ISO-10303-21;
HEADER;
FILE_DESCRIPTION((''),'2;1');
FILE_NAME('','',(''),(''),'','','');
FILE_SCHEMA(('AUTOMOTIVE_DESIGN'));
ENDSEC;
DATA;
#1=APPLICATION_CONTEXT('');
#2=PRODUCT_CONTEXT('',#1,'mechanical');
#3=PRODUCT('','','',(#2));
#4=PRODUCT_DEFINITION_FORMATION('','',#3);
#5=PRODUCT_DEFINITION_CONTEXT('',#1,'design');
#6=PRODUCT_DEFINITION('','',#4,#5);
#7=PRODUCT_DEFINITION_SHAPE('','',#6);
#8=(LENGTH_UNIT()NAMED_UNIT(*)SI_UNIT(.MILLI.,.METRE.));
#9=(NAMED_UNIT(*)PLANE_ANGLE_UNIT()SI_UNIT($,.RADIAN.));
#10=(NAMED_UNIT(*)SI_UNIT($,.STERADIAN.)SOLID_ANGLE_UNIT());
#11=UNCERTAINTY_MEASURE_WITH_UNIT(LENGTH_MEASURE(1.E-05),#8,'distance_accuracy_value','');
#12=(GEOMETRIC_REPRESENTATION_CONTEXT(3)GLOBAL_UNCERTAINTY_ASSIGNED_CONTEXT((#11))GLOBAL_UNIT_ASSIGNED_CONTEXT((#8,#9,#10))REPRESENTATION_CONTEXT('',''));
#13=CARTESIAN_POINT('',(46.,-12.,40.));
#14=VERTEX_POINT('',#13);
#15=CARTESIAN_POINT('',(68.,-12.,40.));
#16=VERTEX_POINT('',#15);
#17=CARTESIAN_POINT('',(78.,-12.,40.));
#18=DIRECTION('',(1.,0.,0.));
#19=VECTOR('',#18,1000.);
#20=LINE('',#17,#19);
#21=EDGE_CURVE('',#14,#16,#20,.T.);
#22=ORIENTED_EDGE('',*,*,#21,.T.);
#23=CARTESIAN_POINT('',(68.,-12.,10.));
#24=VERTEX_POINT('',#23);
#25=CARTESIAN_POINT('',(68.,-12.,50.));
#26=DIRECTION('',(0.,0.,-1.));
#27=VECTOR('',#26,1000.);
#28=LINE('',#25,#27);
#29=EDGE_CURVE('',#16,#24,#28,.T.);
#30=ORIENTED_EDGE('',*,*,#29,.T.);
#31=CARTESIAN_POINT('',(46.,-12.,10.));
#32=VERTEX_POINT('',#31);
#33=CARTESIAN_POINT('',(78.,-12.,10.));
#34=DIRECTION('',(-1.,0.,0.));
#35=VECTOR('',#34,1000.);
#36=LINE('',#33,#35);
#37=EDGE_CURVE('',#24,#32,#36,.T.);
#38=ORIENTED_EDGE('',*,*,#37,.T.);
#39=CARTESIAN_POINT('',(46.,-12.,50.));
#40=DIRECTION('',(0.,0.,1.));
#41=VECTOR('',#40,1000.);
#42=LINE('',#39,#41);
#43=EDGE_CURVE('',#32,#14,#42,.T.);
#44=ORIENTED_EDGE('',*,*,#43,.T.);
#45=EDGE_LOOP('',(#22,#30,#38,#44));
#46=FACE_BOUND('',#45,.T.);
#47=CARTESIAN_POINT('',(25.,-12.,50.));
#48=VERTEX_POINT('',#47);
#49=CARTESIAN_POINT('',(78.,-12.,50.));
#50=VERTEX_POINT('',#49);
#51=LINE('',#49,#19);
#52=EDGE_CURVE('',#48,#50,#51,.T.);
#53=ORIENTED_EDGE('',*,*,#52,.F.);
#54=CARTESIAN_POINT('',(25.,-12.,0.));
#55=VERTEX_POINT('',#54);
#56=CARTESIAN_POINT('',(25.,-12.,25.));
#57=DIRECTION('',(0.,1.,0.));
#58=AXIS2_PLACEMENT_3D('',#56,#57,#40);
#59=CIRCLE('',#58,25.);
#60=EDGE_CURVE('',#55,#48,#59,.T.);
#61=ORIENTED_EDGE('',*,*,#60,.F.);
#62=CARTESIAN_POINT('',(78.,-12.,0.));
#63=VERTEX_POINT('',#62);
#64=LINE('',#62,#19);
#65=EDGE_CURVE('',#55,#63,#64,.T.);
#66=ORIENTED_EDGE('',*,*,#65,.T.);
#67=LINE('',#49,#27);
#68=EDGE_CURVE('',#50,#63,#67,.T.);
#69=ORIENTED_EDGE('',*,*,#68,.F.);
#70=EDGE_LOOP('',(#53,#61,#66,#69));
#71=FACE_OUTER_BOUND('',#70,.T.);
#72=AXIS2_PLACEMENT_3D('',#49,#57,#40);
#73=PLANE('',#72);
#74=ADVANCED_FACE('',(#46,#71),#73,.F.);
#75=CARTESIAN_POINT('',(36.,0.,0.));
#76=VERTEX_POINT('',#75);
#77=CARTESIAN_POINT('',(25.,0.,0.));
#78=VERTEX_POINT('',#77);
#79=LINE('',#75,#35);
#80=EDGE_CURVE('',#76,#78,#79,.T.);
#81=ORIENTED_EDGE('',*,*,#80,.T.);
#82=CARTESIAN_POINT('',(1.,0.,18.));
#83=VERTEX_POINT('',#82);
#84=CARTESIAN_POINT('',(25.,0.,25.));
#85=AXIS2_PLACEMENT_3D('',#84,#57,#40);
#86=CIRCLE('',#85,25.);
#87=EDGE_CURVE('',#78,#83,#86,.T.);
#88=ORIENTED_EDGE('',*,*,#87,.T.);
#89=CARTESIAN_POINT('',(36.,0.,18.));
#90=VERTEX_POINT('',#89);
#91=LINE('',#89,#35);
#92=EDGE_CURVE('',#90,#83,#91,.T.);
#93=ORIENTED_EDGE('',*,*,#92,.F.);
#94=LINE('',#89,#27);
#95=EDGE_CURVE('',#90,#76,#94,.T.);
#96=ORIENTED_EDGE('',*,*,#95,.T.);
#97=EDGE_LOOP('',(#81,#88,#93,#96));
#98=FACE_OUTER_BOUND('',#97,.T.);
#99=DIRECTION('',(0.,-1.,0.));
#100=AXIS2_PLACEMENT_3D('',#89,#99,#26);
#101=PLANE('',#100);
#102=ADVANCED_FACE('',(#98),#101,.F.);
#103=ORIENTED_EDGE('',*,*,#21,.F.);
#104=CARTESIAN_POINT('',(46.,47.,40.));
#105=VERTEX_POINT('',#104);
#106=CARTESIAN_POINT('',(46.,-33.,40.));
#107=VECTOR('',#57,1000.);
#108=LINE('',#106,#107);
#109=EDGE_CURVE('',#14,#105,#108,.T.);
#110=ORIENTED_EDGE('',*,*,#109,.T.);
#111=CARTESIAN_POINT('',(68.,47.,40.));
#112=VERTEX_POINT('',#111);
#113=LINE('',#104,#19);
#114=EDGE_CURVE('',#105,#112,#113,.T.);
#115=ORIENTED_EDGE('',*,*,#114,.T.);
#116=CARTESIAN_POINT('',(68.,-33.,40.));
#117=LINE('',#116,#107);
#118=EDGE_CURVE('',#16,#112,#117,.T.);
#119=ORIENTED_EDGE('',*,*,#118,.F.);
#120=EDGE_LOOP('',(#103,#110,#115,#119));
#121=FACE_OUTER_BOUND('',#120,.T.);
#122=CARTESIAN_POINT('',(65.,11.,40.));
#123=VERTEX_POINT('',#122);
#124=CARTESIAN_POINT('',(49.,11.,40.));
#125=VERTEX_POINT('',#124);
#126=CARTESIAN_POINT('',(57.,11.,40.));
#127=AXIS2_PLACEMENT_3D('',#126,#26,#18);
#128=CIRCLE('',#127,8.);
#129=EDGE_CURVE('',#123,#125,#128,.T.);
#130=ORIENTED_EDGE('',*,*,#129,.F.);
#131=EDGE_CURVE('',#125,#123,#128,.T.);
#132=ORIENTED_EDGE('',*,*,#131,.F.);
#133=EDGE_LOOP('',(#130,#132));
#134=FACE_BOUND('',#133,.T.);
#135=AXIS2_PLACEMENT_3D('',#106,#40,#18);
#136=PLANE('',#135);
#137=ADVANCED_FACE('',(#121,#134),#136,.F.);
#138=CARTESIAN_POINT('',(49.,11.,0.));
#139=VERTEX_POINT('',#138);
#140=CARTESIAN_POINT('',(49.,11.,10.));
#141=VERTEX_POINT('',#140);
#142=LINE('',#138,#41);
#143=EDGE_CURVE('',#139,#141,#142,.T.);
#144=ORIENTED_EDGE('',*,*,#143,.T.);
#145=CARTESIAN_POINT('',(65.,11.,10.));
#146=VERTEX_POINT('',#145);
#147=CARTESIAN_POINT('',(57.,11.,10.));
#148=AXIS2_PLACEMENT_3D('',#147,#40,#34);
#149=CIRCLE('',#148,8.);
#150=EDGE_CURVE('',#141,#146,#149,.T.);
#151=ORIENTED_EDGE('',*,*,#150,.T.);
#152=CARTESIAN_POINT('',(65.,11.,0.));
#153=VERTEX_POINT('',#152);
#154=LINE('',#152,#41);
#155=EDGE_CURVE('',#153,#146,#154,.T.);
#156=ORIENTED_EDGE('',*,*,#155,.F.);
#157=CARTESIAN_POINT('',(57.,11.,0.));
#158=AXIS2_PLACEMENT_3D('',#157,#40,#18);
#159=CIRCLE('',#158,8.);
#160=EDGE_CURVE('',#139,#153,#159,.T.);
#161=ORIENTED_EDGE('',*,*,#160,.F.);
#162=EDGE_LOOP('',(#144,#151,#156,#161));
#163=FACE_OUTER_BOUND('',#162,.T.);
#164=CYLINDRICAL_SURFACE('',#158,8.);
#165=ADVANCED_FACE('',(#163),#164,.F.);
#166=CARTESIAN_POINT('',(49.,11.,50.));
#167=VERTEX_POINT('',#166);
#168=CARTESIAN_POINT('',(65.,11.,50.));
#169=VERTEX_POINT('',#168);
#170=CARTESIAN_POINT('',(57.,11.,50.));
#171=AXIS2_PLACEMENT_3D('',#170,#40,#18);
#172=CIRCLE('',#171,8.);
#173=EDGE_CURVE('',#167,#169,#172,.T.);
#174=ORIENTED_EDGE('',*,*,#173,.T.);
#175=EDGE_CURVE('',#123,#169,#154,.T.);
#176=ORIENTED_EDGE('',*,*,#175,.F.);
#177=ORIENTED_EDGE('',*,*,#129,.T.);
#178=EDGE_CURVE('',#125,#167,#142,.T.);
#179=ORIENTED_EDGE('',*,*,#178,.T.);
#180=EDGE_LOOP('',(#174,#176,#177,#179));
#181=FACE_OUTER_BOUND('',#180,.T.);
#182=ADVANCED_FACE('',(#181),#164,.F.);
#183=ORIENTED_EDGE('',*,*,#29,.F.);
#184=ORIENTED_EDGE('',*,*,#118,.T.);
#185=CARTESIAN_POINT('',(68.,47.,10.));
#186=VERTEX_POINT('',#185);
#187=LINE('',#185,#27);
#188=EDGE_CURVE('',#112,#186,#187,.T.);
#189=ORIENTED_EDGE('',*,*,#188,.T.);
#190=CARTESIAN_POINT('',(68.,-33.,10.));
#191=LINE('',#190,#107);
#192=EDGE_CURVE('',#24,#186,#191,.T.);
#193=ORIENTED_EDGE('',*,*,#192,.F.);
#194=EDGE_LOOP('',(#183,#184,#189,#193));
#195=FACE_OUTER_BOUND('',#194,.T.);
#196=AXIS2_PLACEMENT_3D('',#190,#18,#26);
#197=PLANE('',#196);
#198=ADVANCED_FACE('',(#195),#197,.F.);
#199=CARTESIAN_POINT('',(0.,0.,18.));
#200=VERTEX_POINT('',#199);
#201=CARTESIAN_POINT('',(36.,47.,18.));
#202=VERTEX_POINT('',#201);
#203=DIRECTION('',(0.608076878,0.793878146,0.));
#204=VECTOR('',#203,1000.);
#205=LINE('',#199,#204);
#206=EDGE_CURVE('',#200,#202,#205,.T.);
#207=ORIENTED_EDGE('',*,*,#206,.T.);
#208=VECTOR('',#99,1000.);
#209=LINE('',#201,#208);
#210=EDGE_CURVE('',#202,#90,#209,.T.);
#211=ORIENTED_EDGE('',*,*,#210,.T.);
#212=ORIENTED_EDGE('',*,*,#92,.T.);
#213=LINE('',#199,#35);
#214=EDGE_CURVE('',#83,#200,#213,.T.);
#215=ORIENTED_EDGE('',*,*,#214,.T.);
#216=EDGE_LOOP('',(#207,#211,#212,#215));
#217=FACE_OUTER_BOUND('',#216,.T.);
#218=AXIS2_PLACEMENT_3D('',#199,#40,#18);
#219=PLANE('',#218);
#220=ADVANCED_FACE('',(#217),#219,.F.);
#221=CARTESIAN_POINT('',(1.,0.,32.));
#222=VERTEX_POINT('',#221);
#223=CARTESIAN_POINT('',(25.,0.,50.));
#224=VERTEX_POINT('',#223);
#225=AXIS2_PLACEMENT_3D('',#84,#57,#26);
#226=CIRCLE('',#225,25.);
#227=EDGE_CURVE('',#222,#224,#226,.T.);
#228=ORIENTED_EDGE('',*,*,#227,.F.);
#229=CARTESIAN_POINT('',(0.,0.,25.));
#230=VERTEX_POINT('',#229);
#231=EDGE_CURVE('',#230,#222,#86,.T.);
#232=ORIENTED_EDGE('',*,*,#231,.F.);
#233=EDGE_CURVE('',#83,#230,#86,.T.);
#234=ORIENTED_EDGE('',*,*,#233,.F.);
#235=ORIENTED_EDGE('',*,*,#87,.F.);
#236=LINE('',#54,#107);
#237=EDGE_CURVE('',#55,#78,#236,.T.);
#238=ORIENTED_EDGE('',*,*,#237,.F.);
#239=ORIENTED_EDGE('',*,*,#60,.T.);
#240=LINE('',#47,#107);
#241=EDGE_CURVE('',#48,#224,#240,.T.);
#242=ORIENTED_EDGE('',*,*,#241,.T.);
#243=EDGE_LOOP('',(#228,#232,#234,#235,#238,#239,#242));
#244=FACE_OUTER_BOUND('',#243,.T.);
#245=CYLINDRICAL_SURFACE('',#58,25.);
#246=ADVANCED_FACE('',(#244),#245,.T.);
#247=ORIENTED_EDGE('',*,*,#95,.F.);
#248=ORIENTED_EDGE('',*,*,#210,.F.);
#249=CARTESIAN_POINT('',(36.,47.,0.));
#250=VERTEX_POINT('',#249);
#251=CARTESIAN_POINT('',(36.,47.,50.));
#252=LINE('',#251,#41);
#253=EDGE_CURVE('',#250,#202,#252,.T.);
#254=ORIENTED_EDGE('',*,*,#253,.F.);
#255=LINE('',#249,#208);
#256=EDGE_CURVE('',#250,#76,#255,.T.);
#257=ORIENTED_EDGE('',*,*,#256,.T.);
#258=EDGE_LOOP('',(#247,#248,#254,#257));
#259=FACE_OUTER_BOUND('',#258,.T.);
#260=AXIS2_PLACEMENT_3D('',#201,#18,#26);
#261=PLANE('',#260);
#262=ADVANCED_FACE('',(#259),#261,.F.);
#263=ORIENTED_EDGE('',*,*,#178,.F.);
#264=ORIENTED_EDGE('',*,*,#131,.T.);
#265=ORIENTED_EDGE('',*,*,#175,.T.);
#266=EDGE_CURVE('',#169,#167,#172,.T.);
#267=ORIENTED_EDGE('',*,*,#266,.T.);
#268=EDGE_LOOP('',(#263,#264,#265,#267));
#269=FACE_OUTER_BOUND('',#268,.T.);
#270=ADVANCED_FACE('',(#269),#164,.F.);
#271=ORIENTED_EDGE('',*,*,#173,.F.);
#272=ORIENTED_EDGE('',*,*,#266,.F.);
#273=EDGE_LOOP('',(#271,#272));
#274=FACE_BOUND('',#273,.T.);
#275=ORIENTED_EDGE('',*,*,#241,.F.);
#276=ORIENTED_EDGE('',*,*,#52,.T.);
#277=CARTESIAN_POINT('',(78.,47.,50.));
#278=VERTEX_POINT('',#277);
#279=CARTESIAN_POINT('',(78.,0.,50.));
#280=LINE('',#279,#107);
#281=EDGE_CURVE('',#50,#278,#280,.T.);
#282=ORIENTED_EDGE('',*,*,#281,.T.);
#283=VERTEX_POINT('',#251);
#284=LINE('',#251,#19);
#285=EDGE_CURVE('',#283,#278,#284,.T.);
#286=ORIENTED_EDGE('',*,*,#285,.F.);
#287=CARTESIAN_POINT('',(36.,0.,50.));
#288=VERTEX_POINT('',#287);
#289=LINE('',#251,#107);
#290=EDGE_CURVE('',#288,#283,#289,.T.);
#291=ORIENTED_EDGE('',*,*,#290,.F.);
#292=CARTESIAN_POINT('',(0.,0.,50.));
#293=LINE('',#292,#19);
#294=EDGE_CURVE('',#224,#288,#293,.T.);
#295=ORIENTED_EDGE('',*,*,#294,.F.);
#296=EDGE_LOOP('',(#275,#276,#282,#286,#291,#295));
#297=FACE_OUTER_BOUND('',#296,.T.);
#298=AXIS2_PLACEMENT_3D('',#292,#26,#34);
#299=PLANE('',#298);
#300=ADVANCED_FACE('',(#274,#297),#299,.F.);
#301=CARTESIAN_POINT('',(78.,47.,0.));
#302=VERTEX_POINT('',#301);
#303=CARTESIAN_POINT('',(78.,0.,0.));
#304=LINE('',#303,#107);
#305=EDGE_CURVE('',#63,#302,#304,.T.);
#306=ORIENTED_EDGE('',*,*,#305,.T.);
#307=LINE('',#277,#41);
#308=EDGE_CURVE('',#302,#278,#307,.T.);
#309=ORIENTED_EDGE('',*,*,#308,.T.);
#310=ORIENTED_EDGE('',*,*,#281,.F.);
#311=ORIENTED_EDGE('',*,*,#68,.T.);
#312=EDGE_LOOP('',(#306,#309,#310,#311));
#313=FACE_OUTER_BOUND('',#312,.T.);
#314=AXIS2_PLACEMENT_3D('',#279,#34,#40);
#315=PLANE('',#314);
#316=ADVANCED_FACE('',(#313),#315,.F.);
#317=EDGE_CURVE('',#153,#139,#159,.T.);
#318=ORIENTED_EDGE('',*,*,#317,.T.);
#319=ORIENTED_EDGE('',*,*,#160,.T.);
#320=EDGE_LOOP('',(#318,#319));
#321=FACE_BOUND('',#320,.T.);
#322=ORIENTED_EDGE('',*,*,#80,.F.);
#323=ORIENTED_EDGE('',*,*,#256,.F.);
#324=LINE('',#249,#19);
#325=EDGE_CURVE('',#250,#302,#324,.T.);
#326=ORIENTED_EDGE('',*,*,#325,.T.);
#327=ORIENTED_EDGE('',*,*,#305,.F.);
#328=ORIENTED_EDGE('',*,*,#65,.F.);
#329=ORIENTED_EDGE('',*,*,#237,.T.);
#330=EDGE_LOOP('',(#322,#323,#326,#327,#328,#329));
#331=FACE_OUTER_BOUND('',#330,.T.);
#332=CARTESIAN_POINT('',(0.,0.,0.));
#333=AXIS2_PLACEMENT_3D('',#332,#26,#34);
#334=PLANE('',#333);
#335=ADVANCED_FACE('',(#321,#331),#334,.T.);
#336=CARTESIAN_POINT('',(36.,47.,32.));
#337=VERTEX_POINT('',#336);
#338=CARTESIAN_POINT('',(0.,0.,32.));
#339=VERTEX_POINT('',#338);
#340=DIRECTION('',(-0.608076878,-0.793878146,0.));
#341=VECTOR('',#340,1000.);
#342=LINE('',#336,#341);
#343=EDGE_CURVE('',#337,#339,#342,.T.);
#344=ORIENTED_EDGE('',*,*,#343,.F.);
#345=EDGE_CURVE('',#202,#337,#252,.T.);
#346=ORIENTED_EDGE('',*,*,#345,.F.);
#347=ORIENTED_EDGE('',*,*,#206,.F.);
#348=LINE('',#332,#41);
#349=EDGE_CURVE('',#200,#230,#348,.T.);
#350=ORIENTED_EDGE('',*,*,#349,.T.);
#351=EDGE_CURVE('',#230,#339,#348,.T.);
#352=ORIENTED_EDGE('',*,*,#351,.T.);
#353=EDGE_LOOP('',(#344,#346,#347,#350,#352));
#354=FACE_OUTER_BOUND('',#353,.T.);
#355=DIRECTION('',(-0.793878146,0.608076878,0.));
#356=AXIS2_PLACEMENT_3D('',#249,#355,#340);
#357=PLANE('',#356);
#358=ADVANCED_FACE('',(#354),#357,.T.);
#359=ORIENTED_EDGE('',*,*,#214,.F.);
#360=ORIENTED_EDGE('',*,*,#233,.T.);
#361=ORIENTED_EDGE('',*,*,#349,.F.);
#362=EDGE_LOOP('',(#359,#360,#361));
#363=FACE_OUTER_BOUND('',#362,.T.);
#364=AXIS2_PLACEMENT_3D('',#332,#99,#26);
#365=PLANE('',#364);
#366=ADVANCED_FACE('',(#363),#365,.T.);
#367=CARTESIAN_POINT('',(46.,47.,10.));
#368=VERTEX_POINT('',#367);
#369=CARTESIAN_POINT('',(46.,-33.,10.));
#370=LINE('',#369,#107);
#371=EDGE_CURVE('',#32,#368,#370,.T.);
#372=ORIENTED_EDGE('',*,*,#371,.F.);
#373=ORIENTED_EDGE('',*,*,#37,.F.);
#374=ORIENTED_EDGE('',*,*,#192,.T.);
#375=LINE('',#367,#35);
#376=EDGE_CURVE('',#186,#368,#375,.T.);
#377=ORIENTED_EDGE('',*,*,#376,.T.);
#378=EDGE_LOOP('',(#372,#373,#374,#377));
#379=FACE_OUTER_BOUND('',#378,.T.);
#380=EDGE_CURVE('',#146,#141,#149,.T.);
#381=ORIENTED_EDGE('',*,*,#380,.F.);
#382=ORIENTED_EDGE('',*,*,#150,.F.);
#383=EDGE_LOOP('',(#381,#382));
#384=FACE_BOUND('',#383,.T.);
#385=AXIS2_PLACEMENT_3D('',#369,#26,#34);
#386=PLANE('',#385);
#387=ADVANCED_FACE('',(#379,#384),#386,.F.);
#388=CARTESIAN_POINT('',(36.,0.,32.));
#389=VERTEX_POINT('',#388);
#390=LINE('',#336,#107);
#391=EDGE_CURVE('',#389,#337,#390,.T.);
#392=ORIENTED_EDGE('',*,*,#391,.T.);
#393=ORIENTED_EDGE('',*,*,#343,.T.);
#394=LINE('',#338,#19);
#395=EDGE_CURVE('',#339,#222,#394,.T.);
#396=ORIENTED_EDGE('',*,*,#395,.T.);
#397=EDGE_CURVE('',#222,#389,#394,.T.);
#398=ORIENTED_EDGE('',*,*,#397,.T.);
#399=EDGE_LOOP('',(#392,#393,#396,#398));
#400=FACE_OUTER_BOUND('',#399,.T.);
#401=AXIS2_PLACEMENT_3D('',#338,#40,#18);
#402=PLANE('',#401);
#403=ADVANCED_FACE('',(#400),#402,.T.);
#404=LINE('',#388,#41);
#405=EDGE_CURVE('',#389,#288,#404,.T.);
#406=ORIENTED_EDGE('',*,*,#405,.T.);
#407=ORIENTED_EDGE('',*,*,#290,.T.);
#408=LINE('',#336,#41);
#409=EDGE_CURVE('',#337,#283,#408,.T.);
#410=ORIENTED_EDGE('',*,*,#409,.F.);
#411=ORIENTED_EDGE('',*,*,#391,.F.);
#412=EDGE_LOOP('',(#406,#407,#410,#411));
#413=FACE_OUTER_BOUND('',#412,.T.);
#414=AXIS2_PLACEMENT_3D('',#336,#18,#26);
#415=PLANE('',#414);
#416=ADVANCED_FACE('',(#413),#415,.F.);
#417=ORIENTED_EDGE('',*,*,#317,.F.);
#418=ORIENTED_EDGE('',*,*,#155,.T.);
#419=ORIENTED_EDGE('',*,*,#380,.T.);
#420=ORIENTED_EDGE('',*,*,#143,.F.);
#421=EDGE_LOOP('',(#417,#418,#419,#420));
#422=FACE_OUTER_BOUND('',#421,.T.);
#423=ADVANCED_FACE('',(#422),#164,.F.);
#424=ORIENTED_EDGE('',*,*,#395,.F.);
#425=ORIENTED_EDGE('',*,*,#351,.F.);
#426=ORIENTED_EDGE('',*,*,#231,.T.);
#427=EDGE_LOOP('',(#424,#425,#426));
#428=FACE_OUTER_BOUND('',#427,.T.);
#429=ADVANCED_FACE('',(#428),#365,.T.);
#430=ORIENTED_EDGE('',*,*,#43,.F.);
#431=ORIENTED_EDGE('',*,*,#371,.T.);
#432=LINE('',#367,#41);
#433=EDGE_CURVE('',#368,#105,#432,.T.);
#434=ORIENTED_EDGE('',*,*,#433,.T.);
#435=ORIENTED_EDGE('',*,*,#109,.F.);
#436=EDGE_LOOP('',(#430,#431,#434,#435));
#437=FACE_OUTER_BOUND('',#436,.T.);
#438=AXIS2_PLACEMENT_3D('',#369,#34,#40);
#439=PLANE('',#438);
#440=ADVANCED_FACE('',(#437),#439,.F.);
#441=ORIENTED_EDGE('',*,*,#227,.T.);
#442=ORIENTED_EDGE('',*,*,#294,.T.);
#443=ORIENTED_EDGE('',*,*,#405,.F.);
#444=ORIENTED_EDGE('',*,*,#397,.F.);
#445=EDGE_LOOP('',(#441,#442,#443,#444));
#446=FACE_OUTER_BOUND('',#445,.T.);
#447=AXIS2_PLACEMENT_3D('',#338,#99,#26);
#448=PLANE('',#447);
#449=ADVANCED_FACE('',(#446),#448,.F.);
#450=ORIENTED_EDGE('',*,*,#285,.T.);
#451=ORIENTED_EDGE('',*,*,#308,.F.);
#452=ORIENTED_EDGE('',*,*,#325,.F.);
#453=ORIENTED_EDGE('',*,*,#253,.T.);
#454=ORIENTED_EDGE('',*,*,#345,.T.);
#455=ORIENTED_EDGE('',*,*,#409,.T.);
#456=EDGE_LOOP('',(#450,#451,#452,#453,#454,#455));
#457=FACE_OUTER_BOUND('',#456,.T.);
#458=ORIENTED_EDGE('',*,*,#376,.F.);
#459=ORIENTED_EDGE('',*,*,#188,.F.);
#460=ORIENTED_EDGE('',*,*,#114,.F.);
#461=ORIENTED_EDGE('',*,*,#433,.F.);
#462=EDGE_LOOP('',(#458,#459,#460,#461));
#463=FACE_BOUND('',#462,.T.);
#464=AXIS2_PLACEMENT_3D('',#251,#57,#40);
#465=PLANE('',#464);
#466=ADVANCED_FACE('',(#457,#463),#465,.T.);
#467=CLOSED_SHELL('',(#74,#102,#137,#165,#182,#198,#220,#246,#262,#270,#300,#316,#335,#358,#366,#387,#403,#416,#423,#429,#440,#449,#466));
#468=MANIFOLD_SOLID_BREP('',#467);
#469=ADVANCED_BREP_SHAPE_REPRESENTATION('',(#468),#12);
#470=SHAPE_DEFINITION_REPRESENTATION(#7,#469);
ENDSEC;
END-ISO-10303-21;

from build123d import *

# Parameters (mm, degrees)
BASE_BLOCK_SKETCH_W              = 78
BASE_BLOCK_SKETCH_H              = 12
BASE_BLOCK_DEPTH                 = 50
UPPER_BLOCK_SKETCH_W             = 50
UPPER_BLOCK_SKETCH_H             = 47
UPPER_BLOCK_DEPTH                = 42
STEP_CUT_12MM_DEPTH              = 12
CROSS_HOLE_SKETCH_R              = 8
CROSS_HOLE_DEPTH                 = 50
RECTANGULAR_POCKET_SKETCH_W      = 22
RECTANGULAR_POCKET_SKETCH_H      = 30
RECTANGULAR_THROUGH_POCKET_DEPTH = 80
WEDGE_LUG_DEPTH                  = 50
WEDGE_CUT_A_DEPTH                = 18
WEDGE_CUT_B_DEPTH                = 18


with BuildPart() as part:
    # Base Block Sketch → Base Block (new body)
    with BuildSketch(Plane.XY):
        with Locations((39, -6)):
            Rectangle(BASE_BLOCK_SKETCH_W, BASE_BLOCK_SKETCH_H)
    extrude(amount=BASE_BLOCK_DEPTH)

    # Upper Block Sketch → Upper Block (add)
    with BuildSketch(Plane(origin=(78, 0, 0), x_dir=(0, 0, -1), z_dir=(1, 0, 0))):
        with Locations((-25, 23.5)):
            Rectangle(UPPER_BLOCK_SKETCH_W, UPPER_BLOCK_SKETCH_H)
    extrude(amount=-UPPER_BLOCK_DEPTH)

    # Step Cut Sketch → Step Cut 12mm (cut)
    with BuildSketch(Plane(origin=(0, 0, 0), x_dir=(1, 0, 0), z_dir=(0, 1, 0))):
        with BuildLine():
            Line((25, 0), (0, 0))
            Line((0, 0), (0, -25))
            ThreePointArc((0, -25), (7.32233047, -7.32233047), (25, 0))
        make_face()
        with BuildLine():
            ThreePointArc((25, -50), (7.32233047, -42.67766953), (0, -25))
            Line((0, -25), (0, -50))
            Line((0, -50), (25, -50))
        make_face()
    extrude(amount=-STEP_CUT_12MM_DEPTH, mode=Mode.SUBTRACT)

    # Cross Hole Sketch → Cross Hole (cut)
    with BuildSketch(Plane.XY.offset(50)):
        with Locations((57, 11)):
            Circle(CROSS_HOLE_SKETCH_R)
    extrude(amount=-CROSS_HOLE_DEPTH, mode=Mode.SUBTRACT)

    # Rectangular Pocket Sketch → Rectangular Through Pocket (cut)
    with BuildSketch(Plane(origin=(0, 47, 0), x_dir=(1, 0, 0), z_dir=(0, 1, 0))):
        with Locations((57, -25)):
            Rectangle(RECTANGULAR_POCKET_SKETCH_W, RECTANGULAR_POCKET_SKETCH_H)
    extrude(amount=-RECTANGULAR_THROUGH_POCKET_DEPTH, mode=Mode.SUBTRACT)

    # Wedge Lug Sketch → Wedge Lug (add)
    with BuildSketch(Plane.XY.offset(50)):
        Polygon((36, 47), (0, 0), (36, 0), align=None)
    extrude(amount=-WEDGE_LUG_DEPTH)

    # Wedge Cut A Sketch → Wedge Cut A (cut)
    with BuildSketch(Plane.XY.offset(50)):
        Polygon((36, 47), (36, 0), (0, 0), align=None)
    extrude(amount=-WEDGE_CUT_A_DEPTH, mode=Mode.SUBTRACT)

    # Wedge Cut B Sketch → Wedge Cut B (cut)
    with BuildSketch(Plane(origin=(0, 0, 0), x_dir=(-1, 0, 0), z_dir=(0, 0, -1))):
        Polygon((-36, 47), (-36, 0), (0, 0), align=None)
    extrude(amount=-WEDGE_CUT_B_DEPTH, mode=Mode.SUBTRACT)


solid = part.part
